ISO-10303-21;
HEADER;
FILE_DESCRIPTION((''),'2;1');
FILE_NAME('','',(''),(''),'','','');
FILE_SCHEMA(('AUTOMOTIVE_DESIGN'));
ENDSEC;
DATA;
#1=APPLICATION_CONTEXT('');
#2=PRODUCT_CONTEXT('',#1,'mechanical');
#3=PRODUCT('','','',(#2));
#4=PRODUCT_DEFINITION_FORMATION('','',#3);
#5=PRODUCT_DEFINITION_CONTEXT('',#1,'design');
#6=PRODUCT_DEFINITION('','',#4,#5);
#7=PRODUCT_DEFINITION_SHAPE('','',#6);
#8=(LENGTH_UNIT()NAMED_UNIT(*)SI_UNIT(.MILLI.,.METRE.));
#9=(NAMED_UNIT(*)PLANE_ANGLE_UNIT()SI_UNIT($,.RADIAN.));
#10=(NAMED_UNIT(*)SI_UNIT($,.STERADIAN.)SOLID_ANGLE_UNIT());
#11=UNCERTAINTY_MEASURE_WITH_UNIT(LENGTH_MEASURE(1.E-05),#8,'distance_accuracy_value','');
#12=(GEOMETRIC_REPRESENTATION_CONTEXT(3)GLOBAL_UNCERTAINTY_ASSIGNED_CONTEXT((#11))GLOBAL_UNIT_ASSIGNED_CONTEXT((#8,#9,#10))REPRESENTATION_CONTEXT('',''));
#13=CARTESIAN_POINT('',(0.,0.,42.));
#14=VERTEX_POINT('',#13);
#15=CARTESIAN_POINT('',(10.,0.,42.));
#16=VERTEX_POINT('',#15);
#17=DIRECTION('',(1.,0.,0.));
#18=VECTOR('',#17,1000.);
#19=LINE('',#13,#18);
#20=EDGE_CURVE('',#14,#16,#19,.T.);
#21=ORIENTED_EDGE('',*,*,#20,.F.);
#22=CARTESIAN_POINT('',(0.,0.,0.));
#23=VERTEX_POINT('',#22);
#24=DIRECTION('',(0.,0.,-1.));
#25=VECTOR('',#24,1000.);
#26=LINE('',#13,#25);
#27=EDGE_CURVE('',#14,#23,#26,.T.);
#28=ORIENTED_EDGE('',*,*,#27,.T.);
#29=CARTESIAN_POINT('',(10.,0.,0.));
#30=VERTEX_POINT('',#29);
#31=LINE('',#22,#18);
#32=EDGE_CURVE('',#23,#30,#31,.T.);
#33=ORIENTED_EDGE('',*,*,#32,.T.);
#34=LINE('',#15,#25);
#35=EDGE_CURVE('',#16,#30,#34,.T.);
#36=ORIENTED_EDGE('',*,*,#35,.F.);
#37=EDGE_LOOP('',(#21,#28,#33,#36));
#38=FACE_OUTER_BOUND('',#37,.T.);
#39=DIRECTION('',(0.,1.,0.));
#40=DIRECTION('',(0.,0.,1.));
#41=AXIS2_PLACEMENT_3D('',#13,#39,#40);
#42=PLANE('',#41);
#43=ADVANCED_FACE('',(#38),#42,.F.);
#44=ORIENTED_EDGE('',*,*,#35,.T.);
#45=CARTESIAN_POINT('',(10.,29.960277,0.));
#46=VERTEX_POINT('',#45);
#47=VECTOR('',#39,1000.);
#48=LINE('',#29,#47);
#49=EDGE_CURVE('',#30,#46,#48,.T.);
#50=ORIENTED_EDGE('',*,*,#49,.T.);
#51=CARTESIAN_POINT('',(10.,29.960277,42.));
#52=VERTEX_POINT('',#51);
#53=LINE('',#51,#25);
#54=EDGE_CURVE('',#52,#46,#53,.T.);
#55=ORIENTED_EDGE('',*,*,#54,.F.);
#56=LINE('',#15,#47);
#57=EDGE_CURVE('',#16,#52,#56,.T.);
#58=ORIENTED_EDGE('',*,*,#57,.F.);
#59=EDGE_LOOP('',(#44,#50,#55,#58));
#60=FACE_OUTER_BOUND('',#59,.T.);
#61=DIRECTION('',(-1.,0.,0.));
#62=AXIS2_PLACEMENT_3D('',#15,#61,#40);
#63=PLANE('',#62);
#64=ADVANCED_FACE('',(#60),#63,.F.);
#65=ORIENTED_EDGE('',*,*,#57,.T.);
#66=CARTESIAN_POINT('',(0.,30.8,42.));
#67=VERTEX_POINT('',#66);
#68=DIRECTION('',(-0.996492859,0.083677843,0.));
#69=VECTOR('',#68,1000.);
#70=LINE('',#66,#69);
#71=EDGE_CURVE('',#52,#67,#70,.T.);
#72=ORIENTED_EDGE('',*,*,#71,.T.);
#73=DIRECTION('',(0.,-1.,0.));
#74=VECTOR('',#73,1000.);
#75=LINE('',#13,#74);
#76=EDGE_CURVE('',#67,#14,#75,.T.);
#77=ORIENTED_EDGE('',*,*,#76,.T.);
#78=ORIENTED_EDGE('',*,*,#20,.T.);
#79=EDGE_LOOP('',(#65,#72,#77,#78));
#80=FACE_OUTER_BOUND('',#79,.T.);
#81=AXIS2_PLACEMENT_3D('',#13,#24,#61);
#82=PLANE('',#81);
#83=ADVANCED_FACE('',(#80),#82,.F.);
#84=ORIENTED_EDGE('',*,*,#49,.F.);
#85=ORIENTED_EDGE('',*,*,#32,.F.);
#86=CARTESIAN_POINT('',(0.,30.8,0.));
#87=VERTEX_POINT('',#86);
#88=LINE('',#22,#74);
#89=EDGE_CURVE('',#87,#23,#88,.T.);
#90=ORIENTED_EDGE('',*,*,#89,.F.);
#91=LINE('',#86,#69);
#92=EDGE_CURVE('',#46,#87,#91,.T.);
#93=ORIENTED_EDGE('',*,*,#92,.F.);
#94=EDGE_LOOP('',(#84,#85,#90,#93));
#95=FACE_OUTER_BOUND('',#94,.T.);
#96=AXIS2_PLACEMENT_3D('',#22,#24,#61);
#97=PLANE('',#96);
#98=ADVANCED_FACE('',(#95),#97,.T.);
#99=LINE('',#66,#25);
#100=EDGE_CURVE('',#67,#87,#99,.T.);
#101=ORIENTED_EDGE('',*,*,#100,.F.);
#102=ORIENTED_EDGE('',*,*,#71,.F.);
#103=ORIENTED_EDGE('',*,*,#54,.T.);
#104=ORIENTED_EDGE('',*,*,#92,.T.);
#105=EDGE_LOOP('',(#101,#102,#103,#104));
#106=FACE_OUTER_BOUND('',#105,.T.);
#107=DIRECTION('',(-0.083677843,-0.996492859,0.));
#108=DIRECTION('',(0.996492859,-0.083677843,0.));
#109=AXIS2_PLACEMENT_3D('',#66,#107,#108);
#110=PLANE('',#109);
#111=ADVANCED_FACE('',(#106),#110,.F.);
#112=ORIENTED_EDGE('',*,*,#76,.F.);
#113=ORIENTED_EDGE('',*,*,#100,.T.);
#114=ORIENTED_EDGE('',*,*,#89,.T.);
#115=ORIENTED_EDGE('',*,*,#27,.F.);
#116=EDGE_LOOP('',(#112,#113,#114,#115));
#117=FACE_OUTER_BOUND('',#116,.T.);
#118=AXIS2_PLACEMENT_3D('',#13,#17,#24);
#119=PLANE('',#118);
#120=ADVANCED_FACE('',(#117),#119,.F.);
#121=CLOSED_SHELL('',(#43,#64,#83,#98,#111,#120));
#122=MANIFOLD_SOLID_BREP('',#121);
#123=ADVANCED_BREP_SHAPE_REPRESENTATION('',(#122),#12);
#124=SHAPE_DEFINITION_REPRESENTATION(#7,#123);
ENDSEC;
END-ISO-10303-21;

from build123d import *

# Parameters (mm, degrees)
BOSS_EXTRUDE1_DEPTH = 42


with BuildPart() as part:
    # Sketch1 → Boss-Extrude1 (new body)
    with BuildSketch(Plane.XY):
        Polygon((0, 30.8), (10, 29.960276538), (10, 0), (0, 0), align=None)
    extrude(amount=BOSS_EXTRUDE1_DEPTH)


solid = part.part
